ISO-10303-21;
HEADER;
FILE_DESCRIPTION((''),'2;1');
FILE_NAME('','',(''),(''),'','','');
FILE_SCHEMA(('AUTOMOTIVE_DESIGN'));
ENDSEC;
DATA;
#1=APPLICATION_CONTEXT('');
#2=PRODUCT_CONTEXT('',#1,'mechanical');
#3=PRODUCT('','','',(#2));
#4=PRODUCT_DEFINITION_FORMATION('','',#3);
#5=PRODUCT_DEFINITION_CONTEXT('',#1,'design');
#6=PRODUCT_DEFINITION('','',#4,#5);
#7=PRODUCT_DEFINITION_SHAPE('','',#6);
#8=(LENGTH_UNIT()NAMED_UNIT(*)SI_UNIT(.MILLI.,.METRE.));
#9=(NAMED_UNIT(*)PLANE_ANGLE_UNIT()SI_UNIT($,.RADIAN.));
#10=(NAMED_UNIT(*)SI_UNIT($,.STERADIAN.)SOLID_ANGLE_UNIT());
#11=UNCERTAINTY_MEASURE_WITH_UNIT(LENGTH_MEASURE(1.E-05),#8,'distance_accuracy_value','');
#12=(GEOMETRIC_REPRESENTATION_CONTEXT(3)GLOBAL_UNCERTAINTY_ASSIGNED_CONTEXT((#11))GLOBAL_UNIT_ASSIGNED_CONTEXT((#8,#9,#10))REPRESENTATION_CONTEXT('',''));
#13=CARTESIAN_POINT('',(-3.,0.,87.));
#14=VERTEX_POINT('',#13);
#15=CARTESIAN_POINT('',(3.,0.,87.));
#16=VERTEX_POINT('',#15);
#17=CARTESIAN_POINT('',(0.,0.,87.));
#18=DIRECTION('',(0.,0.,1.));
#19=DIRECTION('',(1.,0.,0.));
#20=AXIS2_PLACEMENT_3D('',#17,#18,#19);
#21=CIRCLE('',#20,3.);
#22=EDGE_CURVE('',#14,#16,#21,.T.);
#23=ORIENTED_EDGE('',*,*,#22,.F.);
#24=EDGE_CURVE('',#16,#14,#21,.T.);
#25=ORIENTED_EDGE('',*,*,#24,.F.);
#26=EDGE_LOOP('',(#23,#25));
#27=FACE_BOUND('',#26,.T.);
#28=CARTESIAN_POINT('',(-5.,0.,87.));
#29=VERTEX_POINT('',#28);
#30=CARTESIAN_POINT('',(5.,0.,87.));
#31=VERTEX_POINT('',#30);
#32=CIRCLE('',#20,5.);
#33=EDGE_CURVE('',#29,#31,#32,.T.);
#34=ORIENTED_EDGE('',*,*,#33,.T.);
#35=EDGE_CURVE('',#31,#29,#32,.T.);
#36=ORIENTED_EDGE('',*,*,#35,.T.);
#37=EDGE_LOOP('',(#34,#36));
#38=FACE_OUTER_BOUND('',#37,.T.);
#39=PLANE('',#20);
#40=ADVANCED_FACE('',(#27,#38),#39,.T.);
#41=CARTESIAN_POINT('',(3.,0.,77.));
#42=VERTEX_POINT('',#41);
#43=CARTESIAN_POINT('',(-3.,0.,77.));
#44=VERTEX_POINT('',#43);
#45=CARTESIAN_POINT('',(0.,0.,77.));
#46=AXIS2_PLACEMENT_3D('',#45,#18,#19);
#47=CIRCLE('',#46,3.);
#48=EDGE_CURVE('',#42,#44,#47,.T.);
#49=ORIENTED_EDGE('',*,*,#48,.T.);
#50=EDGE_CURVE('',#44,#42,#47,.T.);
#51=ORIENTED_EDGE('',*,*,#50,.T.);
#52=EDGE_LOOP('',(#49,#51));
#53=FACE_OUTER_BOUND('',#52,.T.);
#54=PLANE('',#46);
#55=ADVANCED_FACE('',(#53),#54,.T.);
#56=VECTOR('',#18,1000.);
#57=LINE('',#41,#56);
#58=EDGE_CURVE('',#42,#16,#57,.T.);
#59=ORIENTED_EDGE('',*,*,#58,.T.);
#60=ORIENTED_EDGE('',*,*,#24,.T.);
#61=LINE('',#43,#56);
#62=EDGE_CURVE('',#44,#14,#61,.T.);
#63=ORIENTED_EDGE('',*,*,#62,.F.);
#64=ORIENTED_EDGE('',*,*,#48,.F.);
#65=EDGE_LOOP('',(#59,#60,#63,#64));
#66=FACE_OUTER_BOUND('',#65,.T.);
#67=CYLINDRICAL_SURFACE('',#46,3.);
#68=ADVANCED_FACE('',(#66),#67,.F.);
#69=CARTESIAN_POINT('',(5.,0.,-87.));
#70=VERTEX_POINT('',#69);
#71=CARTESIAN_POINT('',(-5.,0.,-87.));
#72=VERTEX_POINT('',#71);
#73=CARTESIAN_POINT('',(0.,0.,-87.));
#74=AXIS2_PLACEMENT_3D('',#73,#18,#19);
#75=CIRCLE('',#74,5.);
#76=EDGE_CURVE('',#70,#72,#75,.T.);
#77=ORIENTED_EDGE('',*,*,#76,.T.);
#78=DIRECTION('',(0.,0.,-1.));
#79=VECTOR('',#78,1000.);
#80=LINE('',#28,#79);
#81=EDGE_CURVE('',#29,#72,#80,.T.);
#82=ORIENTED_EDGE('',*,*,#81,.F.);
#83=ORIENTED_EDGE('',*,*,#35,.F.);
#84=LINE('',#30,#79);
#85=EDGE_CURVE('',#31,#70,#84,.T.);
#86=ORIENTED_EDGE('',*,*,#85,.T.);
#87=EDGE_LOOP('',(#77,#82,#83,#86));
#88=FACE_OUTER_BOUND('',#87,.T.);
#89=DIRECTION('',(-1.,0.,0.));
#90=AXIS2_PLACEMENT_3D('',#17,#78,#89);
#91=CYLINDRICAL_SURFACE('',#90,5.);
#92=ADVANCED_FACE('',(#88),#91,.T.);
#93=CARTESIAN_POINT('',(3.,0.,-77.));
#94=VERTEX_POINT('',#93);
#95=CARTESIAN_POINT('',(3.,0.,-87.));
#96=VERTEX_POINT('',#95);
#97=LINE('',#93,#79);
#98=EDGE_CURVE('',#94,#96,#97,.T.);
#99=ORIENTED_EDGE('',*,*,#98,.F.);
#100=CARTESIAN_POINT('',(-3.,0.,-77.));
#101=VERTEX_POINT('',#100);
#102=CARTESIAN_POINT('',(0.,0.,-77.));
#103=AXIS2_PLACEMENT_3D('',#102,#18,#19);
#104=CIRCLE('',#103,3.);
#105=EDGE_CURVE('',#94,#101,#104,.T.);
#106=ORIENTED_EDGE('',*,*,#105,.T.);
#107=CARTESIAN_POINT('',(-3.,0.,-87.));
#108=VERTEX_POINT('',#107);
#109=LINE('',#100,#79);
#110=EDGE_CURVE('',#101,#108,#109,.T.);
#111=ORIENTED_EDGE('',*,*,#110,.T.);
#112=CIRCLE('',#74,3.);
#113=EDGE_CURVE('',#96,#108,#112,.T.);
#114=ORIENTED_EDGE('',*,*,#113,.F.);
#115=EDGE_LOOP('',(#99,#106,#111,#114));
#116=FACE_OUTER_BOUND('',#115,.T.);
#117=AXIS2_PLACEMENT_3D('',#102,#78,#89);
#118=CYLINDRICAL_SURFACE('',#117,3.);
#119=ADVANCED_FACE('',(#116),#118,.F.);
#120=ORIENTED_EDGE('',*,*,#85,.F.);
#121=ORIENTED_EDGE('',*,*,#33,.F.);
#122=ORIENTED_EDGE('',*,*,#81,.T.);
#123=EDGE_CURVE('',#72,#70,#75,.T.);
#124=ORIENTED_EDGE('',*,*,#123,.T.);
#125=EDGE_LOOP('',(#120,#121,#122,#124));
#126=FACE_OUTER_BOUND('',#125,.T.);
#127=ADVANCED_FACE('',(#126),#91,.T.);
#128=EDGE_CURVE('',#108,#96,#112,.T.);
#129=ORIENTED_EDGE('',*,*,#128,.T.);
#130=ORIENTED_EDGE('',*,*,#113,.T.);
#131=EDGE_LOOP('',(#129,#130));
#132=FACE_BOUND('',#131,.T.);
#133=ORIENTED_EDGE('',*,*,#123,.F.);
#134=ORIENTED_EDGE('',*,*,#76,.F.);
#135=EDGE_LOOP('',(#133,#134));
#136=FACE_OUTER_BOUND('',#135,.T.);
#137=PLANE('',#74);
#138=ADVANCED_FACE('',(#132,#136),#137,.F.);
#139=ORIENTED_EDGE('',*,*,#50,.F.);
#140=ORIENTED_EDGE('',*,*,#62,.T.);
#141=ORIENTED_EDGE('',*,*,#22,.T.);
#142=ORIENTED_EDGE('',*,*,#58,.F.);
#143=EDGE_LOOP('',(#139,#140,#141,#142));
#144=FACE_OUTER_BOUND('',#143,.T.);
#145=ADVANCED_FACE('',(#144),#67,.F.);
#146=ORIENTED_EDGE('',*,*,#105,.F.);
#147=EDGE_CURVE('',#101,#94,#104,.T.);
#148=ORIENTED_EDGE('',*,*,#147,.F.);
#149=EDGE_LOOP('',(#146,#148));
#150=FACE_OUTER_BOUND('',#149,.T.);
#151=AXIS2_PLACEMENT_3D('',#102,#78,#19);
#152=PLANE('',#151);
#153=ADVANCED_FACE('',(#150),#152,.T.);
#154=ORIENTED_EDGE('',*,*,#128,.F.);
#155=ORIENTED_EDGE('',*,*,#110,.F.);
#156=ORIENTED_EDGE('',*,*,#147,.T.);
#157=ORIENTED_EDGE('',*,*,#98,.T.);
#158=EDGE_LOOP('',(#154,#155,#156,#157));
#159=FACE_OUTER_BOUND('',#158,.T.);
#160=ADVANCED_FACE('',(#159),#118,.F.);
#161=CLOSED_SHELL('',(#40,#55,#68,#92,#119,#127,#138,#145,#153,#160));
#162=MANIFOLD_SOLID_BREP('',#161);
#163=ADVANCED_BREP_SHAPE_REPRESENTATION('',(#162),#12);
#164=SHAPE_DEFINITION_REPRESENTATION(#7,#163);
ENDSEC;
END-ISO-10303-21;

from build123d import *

# Parameters (mm, degrees)
SKETCH1_R           = 5
BOSS_EXTRUDE1_DEPTH = 87
SKETCH2_R           = 3
CUT_EXTRUDE1_DEPTH  = 10


with BuildPart() as part:
    # Sketch1 → Boss-Extrude1 (new, symmetric)
    with BuildSketch(Plane.XY):
        Circle(SKETCH1_R)
    extrude(amount=BOSS_EXTRUDE1_DEPTH, both=True)

    # Sketch2 → Cut-Extrude1 (cut)
    with BuildSketch(Plane.XY.offset(87)):
        Circle(SKETCH2_R)
    cut_extrude1 = extrude(amount=-CUT_EXTRUDE1_DEPTH, mode=Mode.SUBTRACT)

    # Mirror1: Cut-Extrude1 across plane
    add(cut_extrude1.mirror(Plane.XY), mode=Mode.SUBTRACT)


solid = part.part
